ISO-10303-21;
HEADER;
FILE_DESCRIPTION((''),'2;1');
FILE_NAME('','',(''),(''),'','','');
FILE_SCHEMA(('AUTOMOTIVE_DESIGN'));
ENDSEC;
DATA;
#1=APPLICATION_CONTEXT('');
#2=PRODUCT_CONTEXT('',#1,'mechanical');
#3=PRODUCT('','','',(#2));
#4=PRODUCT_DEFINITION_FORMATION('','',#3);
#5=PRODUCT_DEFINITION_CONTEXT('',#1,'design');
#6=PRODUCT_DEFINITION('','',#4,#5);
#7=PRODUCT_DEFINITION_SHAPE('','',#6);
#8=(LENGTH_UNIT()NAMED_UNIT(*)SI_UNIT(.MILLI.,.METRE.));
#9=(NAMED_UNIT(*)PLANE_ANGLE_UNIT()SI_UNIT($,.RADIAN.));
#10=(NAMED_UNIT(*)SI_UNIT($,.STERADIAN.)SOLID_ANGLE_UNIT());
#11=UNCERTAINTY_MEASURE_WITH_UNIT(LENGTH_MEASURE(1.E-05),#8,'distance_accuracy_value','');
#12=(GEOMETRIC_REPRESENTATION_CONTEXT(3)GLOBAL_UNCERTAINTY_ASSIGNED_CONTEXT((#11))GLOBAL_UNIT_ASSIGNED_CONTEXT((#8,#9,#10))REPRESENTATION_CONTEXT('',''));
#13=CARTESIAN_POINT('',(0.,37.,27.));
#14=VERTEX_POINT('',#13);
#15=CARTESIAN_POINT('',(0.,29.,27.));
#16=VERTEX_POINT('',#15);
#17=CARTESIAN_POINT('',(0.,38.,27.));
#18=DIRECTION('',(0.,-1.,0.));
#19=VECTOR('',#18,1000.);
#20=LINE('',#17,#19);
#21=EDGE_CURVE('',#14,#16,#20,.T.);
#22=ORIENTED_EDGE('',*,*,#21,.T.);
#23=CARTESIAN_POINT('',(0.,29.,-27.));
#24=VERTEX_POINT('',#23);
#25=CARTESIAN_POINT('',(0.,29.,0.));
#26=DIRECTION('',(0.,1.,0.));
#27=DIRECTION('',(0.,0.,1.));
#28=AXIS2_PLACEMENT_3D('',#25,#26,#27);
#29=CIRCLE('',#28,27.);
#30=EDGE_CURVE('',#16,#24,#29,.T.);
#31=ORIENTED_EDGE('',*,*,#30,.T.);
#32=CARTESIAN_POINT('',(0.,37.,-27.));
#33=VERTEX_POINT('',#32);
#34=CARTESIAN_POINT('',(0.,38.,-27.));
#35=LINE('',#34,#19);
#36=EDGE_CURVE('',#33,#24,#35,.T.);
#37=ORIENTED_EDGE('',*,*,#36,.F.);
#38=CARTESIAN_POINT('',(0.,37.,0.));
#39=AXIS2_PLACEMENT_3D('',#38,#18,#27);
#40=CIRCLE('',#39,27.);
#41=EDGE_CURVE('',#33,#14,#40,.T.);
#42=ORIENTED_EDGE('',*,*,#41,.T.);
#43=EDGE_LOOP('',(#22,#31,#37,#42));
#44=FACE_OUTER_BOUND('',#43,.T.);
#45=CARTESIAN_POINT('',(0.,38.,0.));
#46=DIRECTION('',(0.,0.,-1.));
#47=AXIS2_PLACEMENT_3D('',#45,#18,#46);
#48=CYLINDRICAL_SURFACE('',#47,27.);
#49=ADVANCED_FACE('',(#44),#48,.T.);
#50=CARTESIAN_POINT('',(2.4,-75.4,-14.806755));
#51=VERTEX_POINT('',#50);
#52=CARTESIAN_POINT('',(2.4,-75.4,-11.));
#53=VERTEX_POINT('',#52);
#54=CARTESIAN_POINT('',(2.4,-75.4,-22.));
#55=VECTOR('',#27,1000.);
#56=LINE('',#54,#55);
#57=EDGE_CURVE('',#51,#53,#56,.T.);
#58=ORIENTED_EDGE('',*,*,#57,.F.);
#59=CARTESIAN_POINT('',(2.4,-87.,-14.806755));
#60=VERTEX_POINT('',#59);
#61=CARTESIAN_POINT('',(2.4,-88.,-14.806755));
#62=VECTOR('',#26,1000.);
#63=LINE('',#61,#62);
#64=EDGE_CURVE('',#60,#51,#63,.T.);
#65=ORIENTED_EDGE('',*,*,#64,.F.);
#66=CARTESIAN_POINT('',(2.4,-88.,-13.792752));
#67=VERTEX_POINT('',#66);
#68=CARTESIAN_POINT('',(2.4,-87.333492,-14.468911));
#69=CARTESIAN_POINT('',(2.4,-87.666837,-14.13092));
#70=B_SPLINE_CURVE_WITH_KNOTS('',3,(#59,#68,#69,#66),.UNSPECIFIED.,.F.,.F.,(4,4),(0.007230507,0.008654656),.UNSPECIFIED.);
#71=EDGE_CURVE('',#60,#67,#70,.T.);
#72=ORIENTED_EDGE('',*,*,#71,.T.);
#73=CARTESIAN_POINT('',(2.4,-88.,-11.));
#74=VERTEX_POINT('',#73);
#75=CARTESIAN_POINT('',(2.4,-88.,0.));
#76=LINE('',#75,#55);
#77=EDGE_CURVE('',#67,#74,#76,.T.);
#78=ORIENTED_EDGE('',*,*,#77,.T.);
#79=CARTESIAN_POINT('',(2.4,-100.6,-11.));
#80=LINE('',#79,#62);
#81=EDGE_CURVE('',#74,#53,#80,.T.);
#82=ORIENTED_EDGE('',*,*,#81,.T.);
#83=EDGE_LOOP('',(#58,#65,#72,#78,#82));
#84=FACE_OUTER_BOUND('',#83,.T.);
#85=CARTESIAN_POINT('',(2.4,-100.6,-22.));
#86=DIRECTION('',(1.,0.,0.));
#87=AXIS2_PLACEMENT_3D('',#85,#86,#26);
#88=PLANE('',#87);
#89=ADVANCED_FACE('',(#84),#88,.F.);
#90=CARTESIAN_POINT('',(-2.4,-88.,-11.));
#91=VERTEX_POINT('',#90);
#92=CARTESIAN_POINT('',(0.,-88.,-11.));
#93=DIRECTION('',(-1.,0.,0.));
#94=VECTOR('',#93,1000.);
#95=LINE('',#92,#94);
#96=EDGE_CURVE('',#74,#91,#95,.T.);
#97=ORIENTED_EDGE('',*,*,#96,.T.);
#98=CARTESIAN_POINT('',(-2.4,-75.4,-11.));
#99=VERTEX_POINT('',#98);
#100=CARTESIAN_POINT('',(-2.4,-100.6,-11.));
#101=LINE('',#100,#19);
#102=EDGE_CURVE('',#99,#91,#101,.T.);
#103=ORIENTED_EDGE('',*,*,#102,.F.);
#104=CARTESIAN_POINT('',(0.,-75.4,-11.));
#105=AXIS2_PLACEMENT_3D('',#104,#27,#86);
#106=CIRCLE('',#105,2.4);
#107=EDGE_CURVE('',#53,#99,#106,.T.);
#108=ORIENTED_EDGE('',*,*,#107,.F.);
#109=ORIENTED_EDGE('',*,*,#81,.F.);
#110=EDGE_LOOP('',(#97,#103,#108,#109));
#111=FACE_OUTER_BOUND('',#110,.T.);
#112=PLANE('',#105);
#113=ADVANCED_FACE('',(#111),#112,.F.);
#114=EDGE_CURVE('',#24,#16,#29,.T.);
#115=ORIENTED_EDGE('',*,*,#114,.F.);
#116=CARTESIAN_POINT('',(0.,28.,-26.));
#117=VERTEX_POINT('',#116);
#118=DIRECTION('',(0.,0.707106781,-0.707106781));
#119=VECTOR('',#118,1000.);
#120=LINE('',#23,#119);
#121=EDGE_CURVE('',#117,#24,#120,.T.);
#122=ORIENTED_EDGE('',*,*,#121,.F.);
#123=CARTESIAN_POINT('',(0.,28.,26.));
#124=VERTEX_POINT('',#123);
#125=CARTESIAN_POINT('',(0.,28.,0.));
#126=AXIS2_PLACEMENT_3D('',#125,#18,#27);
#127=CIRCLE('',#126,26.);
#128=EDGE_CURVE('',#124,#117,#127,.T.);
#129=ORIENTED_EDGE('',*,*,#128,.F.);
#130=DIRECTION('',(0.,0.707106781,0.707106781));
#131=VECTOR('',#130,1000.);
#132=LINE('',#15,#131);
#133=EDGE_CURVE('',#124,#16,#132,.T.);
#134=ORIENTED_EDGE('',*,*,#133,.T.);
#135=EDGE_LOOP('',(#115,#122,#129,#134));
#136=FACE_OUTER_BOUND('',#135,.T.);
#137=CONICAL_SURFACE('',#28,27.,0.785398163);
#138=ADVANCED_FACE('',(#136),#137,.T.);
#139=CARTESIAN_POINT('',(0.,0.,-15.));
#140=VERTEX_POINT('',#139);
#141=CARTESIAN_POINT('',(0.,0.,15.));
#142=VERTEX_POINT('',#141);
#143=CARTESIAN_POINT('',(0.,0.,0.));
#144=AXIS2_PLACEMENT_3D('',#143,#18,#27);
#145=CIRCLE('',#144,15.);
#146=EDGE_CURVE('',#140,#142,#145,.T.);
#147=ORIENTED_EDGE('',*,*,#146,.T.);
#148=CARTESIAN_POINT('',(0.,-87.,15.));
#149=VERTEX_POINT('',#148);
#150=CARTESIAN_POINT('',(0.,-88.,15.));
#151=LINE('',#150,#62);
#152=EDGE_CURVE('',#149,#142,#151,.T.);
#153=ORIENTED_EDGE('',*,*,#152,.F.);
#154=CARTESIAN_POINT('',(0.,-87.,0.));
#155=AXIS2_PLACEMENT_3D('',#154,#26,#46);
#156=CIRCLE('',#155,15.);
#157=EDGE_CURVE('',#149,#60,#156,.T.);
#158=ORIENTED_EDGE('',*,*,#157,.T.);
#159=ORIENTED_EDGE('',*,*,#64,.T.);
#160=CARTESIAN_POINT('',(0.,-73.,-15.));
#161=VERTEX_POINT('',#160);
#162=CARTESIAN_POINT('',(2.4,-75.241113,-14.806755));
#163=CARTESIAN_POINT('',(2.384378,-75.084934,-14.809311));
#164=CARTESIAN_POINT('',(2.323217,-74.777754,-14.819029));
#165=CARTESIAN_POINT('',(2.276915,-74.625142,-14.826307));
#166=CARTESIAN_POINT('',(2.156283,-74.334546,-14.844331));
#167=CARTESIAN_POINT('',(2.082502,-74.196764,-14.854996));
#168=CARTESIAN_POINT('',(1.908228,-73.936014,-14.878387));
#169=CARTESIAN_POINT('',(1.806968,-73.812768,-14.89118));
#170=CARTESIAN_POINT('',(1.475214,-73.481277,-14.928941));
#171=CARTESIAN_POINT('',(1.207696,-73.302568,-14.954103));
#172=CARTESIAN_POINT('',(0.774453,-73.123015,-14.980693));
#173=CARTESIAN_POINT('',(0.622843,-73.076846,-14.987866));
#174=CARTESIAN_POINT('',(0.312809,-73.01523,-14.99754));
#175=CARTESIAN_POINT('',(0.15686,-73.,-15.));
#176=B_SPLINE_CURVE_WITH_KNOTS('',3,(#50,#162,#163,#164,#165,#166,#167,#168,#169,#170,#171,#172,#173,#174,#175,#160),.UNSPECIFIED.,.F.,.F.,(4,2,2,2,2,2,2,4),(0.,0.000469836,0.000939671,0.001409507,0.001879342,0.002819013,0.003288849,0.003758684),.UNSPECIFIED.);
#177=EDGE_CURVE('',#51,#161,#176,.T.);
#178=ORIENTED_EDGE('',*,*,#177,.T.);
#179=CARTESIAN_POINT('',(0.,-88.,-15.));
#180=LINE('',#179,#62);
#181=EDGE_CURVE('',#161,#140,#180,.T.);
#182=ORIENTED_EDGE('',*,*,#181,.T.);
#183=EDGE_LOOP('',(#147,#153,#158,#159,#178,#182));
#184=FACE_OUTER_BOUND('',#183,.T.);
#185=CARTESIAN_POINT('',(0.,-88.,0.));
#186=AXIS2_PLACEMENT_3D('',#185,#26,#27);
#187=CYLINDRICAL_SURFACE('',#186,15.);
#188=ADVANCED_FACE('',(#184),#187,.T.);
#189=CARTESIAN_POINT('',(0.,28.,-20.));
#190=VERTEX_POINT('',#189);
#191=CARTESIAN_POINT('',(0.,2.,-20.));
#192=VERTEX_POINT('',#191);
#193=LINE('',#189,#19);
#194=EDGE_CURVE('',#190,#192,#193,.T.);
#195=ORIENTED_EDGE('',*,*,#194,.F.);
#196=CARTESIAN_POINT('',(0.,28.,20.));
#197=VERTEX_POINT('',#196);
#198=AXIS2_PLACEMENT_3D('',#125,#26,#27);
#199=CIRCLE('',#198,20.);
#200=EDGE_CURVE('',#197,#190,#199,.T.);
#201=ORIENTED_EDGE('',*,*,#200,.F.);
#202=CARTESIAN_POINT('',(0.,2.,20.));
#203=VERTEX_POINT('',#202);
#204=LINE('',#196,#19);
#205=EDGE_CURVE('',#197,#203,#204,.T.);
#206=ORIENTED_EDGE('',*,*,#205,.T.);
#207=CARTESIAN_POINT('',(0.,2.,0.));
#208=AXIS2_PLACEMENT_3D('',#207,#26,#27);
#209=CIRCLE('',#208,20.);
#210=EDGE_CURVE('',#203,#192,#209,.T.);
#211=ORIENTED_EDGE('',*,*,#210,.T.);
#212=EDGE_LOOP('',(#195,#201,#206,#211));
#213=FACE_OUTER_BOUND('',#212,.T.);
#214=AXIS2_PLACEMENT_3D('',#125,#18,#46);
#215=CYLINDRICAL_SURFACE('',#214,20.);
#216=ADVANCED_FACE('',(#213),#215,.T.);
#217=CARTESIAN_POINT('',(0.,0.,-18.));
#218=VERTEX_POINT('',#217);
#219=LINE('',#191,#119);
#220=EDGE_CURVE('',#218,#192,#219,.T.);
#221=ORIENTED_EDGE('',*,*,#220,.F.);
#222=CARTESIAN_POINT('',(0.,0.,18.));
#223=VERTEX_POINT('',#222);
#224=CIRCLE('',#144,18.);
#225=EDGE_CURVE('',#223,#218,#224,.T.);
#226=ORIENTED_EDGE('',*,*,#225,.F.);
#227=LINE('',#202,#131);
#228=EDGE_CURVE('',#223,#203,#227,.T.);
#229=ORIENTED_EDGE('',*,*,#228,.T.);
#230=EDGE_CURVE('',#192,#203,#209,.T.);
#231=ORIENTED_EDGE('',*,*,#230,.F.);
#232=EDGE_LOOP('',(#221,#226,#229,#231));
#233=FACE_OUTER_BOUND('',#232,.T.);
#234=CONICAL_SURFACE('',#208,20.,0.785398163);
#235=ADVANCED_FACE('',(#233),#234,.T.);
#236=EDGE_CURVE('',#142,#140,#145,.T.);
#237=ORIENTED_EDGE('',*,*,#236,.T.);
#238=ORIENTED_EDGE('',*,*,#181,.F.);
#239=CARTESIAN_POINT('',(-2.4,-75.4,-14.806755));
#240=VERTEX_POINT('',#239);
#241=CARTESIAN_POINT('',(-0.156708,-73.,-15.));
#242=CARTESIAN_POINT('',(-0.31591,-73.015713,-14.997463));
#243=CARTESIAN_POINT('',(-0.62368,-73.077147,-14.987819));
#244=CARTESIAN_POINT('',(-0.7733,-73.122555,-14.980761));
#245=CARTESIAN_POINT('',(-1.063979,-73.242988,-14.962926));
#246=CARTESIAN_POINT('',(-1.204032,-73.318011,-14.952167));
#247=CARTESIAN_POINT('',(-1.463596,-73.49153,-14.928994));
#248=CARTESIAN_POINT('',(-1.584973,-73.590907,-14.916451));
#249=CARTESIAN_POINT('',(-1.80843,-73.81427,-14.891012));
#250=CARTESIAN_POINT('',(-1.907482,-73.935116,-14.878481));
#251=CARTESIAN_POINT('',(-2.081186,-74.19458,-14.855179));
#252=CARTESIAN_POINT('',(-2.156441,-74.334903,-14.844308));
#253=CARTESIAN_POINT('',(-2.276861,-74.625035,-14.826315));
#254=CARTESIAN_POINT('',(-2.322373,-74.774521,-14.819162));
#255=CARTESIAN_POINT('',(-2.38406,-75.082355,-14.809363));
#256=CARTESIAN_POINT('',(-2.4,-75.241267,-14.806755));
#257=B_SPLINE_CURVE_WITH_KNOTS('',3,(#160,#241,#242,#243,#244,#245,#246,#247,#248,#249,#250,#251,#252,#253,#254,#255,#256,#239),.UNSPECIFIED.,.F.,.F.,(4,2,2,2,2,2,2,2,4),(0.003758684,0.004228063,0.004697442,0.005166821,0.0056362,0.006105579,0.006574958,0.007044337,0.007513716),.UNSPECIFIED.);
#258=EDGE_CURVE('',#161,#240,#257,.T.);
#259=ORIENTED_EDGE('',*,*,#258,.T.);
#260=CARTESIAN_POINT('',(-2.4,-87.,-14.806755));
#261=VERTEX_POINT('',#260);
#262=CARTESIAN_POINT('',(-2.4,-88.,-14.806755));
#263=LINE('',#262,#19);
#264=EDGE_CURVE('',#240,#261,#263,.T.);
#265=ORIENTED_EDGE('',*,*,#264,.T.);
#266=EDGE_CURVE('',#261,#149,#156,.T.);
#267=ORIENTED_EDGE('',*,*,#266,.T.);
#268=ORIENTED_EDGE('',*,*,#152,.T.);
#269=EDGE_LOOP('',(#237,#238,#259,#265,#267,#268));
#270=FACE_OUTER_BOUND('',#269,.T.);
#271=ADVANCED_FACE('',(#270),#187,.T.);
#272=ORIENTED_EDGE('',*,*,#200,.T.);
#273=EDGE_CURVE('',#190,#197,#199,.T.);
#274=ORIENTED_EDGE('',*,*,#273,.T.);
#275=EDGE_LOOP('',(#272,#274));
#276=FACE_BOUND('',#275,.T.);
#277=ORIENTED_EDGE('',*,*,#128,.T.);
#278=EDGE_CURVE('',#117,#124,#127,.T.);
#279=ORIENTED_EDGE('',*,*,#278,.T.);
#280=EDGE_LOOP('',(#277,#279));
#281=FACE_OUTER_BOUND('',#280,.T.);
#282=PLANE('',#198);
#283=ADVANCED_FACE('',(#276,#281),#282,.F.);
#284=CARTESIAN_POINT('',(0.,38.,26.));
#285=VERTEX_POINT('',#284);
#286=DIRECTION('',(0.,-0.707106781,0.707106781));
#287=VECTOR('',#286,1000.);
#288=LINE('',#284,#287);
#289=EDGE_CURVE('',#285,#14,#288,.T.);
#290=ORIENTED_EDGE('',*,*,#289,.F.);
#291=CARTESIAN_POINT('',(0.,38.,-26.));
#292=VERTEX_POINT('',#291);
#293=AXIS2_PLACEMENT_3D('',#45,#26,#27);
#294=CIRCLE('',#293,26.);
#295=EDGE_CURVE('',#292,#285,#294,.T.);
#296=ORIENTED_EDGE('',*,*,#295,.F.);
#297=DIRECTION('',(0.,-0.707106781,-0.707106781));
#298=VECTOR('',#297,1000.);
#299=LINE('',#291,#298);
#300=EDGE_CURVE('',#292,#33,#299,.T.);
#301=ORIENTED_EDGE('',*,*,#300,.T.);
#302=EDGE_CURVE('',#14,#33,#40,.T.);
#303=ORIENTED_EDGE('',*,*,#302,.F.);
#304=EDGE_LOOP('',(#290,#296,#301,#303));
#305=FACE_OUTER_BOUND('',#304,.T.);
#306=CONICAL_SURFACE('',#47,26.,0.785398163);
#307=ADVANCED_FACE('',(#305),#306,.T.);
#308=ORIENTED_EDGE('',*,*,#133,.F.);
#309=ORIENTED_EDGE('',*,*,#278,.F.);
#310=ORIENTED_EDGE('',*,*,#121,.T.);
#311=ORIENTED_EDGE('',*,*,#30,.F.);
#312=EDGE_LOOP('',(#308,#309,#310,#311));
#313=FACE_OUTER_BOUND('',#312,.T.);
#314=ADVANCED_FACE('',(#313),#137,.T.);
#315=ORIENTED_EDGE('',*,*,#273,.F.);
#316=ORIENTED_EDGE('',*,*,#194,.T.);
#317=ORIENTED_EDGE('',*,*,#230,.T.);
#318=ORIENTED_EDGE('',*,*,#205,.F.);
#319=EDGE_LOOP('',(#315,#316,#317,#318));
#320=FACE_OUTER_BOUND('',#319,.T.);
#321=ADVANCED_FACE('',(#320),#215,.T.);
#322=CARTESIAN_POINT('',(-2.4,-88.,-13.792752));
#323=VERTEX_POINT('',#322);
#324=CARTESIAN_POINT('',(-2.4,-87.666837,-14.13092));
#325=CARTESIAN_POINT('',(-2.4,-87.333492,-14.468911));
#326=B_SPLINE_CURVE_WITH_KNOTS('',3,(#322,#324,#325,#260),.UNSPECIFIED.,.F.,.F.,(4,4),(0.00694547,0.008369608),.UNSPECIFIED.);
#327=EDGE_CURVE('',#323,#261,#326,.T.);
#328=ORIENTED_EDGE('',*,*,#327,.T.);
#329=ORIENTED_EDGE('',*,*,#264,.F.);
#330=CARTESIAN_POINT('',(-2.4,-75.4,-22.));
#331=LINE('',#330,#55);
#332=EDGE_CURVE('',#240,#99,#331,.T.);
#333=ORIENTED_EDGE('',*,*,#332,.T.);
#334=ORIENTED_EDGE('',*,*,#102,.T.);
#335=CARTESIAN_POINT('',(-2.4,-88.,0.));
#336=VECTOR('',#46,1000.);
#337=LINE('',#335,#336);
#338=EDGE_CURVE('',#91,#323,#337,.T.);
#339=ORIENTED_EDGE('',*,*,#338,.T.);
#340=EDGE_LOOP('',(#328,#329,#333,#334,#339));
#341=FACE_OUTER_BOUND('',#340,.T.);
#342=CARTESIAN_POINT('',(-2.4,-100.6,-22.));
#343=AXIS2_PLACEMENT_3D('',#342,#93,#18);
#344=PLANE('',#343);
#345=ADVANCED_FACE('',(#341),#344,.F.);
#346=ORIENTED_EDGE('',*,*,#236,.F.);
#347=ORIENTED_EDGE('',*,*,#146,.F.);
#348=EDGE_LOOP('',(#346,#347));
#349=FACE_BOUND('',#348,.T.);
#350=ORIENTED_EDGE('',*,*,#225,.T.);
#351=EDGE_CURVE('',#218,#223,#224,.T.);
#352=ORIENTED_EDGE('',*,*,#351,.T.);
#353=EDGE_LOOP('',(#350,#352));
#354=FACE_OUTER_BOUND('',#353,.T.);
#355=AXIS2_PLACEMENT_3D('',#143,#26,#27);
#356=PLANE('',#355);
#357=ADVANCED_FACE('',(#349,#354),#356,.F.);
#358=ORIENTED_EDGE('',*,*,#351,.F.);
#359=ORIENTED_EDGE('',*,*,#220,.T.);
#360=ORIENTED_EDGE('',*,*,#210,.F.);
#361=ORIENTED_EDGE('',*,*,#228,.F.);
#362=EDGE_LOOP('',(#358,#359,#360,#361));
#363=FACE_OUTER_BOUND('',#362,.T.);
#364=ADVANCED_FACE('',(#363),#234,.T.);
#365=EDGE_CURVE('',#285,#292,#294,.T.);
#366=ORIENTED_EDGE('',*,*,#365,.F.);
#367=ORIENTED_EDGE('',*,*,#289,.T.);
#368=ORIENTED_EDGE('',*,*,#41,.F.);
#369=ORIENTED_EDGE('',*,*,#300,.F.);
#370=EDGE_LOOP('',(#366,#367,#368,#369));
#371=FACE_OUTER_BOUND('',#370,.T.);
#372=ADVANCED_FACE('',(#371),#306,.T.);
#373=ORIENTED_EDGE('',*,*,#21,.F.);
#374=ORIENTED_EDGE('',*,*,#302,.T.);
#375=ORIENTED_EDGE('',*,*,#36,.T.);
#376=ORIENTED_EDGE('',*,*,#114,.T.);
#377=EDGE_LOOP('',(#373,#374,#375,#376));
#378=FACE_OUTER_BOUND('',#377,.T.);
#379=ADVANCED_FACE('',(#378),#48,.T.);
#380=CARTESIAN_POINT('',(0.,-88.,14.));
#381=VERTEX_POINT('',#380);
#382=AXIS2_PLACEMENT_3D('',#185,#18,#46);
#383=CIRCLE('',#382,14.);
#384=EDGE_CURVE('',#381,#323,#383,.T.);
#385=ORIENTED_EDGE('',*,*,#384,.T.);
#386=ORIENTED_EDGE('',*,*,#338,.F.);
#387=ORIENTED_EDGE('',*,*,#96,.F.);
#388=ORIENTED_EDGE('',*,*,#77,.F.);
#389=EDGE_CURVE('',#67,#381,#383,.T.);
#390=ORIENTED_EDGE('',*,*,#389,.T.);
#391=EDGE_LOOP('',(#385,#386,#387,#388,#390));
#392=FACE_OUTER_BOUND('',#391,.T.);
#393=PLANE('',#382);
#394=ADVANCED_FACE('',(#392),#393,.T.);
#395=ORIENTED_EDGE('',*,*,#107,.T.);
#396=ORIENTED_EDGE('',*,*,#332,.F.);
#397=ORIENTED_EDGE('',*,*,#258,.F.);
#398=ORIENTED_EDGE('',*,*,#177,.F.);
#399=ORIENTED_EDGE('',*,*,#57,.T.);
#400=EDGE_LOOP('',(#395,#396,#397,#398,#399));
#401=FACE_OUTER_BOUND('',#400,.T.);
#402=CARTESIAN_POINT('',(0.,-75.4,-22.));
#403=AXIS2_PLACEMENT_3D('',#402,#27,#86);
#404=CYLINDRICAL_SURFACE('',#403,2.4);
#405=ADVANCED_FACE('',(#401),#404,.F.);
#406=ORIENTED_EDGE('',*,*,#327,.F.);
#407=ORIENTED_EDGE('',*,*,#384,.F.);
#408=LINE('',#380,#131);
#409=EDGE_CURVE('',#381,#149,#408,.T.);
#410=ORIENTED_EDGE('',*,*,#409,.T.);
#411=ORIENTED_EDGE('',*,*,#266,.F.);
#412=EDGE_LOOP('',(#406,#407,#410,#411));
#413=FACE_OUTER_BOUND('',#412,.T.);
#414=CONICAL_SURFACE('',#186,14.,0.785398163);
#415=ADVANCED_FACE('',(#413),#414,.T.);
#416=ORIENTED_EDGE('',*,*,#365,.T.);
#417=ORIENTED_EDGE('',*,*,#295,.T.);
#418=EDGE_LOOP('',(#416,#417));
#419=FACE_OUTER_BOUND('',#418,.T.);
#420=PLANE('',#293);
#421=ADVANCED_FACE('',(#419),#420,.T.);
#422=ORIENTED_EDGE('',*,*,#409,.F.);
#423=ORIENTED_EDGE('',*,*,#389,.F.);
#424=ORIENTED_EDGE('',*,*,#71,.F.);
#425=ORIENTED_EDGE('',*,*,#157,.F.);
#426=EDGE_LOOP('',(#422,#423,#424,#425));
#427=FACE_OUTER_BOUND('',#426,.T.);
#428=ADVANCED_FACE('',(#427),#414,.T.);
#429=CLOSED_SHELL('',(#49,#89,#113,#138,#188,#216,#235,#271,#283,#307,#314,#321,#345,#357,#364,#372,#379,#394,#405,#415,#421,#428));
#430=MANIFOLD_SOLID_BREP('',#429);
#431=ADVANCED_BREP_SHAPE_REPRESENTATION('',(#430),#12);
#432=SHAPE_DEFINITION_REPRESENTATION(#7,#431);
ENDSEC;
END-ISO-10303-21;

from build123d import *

# Parameters (mm, degrees)
SKETCH1_R           = 20
BOSS_EXTRUDE1_DEPTH = 28
SKETCH2_R           = 27
BOSS_EXTRUDE2_DEPTH = 10
SKETCH3_R           = 15
BOSS_EXTRUDE3_DEPTH = 88
CHAMFER1_SIZE       = 1
CHAMFER2_SIZE       = 2
CUT_EXTRUDE2_START  = -11
CUT_EXTRUDE2_DEPTH  = 11


with BuildPart() as part:
    # Sketch1 → Boss-Extrude1 (new body)
    with BuildSketch(Plane(origin=(0, 0, 0), x_dir=(1, 0, 0), z_dir=(0, 1, 0))):
        with Locations(Location((0, 0, 0), (0, 0, 270))):
            Circle(SKETCH1_R)
    extrude(amount=BOSS_EXTRUDE1_DEPTH)

    # Sketch2 → Boss-Extrude2 (add)
    with BuildSketch(Plane(origin=(0, 28, 0), x_dir=(1, 0, 0), z_dir=(0, 1, 0))):
        with Locations(Location((0, 0, 0), (0, 0, 270))):
            Circle(SKETCH2_R)
    extrude(amount=BOSS_EXTRUDE2_DEPTH)

    # Sketch3 → Boss-Extrude3 (add)
    with BuildSketch(Plane.XZ):
        with Locations(Location((0, 0, 0), (0, 0, 90))):
            Circle(SKETCH3_R)
    extrude(amount=BOSS_EXTRUDE3_DEPTH)

    # Chamfer1
    chamfer1_edges = [part.edges().sort_by_distance(p)[0] for p in [
        (0, -88, -15),
        (0, 28, -27),
        (0, 38, -27),
    ]]
    chamfer(chamfer1_edges, length=CHAMFER1_SIZE)

    # Chamfer2
    chamfer2_edges = [part.edges().sort_by_distance(p)[0] for p in [
        (0, 0, -20),
    ]]
    chamfer(chamfer2_edges, length=CHAMFER2_SIZE)

    # Sketch5 → Cut-Extrude2 (cut)
    with BuildSketch(Plane.XY.offset(CUT_EXTRUDE2_START)):
        with BuildLine():
            Line((-2.4, -100.6), (2.4, -100.6))
            Line((2.4, -100.6), (2.4, -75.4))
            ThreePointArc((2.4, -75.4), (0, -73), (-2.4, -75.4))
            Line((-2.4, -75.4), (-2.4, -100.6))
        make_face()
    extrude(amount=-CUT_EXTRUDE2_DEPTH, mode=Mode.SUBTRACT)


solid = part.part
